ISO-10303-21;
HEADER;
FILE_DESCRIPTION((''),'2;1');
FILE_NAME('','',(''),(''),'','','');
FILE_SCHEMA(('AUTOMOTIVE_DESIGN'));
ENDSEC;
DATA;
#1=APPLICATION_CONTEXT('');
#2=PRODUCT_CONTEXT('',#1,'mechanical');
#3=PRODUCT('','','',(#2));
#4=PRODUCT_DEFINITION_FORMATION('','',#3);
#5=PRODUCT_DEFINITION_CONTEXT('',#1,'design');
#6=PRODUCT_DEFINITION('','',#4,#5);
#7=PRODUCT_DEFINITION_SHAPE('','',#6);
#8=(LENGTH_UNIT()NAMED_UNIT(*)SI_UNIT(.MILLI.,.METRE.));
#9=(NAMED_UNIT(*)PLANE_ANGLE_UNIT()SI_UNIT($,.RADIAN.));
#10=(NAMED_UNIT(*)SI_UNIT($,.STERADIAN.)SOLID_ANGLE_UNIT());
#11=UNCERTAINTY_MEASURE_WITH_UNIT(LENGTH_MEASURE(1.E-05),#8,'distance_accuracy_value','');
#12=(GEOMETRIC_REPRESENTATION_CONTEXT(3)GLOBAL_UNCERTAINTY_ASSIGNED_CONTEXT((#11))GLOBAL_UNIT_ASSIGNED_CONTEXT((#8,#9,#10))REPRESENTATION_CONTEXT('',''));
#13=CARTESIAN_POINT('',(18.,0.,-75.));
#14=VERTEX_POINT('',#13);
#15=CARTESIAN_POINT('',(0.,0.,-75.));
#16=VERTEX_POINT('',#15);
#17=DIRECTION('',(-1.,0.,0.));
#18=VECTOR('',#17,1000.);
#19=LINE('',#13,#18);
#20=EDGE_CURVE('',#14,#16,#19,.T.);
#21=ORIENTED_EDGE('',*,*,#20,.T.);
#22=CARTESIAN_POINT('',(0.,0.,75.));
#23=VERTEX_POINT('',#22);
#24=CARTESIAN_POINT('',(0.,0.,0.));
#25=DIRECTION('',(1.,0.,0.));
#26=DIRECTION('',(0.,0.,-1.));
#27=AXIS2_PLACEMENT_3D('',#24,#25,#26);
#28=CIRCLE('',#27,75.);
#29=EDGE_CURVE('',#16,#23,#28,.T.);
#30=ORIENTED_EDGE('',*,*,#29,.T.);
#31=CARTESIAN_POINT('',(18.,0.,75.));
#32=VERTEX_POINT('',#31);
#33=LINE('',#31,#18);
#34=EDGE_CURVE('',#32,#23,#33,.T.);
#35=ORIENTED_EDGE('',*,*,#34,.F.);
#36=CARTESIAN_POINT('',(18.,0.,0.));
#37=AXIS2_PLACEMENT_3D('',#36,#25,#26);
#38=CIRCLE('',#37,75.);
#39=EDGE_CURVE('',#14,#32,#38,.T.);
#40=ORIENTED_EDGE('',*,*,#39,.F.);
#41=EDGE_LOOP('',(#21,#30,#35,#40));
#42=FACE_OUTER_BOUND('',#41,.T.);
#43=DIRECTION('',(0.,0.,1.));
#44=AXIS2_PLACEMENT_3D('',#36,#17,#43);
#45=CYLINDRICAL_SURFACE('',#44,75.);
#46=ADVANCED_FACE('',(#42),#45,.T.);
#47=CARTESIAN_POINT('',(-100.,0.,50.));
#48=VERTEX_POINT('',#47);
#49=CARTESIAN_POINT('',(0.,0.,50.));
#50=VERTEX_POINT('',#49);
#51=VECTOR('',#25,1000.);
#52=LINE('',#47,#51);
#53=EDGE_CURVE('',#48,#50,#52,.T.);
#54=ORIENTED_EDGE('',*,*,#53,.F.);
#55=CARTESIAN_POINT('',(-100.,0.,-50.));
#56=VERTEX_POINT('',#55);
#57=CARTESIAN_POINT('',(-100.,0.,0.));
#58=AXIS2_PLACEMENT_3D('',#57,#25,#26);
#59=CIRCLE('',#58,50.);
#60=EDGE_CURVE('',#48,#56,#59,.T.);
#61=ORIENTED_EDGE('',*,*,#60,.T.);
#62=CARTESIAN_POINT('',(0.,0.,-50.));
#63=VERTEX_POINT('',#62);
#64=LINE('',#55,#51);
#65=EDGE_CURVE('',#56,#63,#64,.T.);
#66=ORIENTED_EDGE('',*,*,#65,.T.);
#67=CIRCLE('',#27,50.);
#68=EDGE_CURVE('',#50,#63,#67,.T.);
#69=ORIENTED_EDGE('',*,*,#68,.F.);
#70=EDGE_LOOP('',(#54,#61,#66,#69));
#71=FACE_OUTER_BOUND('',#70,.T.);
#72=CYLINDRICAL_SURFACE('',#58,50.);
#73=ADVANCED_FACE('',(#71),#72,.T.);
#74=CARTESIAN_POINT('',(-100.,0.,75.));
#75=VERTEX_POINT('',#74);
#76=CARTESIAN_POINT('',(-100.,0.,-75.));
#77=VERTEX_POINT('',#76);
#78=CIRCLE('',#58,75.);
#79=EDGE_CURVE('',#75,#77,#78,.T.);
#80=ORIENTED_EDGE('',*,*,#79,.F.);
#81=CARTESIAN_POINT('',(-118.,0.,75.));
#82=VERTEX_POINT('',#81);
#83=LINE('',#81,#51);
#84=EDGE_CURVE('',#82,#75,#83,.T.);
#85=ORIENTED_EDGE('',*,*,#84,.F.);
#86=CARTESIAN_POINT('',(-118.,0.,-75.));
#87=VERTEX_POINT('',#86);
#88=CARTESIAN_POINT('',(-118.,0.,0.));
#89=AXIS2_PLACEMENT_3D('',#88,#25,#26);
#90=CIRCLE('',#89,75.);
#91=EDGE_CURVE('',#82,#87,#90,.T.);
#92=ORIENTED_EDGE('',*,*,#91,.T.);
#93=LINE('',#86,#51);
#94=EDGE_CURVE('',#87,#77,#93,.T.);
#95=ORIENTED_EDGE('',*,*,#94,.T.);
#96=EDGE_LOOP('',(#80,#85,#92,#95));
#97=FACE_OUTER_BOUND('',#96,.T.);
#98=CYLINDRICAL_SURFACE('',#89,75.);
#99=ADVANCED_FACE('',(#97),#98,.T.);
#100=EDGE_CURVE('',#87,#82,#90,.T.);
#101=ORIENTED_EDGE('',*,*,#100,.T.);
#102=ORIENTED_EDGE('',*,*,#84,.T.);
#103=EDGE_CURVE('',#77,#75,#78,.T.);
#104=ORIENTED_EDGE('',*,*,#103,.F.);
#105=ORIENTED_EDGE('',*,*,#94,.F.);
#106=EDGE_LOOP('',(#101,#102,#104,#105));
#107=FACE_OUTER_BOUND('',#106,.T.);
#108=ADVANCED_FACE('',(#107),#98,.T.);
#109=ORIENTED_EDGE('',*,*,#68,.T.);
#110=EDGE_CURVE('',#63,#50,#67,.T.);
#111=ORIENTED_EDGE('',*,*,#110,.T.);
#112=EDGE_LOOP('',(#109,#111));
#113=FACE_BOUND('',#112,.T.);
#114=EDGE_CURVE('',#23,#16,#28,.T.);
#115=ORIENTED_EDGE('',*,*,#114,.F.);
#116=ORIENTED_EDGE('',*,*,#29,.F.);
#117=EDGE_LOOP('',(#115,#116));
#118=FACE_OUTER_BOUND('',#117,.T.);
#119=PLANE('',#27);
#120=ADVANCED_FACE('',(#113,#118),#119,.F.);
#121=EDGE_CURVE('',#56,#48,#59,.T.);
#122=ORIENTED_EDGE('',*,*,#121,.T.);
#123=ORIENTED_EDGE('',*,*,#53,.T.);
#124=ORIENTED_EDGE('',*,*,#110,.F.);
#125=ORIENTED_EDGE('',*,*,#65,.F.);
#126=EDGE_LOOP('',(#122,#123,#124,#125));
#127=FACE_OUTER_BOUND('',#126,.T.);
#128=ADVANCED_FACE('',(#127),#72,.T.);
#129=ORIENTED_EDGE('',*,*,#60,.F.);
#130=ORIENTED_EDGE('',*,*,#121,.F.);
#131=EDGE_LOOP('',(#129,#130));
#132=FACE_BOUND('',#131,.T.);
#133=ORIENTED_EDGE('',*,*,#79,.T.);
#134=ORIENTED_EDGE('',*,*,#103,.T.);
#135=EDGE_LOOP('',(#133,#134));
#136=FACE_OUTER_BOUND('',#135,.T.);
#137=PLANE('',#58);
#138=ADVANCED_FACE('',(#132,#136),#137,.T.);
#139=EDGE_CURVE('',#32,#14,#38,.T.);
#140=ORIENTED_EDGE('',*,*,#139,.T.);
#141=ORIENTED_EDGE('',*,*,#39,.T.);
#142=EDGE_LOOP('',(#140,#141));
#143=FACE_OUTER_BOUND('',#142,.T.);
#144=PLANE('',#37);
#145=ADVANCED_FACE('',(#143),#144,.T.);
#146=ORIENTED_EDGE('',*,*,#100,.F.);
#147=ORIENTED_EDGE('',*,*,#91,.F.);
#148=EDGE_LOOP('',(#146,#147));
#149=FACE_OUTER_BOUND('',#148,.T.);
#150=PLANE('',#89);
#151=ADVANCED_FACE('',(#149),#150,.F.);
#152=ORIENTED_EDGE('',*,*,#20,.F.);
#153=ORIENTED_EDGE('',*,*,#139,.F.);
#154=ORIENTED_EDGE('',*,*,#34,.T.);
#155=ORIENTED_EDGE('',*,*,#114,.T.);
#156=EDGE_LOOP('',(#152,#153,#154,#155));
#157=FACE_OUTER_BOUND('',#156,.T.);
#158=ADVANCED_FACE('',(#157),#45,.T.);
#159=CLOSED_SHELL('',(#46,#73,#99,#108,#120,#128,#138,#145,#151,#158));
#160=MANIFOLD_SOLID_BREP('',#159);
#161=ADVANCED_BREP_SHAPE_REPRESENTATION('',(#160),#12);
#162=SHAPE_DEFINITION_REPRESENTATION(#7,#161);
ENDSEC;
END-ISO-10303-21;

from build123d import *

# Parameters (mm, degrees)
SKETCH_1_4_R        = 75
BOSS_EXTRUDE1_DEPTH = 18
SKETCH_1_3_R        = 50
BOSS_EXTRUDE2_DEPTH = 100
BOSS_EXTRUDE3_START = -118
SKETCH_1_4_2_R      = 75
BOSS_EXTRUDE3_DEPTH = 18


with BuildPart() as part:
    # Sketch 1_4 → Boss-Extrude1 (new body)
    with BuildSketch(Plane(origin=(0, 0, 0), x_dir=(0, 0, -1), z_dir=(1, 0, 0))):
        Circle(SKETCH_1_4_R)
    extrude(amount=BOSS_EXTRUDE1_DEPTH)

    # 草图1<3> → Boss-Extrude2 (add)
    with BuildSketch(Plane(origin=(0, 0, 0), x_dir=(0, 0, -1), z_dir=(1, 0, 0))):
        Circle(SKETCH_1_3_R)
    extrude(amount=-BOSS_EXTRUDE2_DEPTH)

    # Sketch 1_4 2 → Boss-Extrude3 (add)
    with BuildSketch(Plane(origin=(0, 0, 0), x_dir=(0, 0, -1), z_dir=(1, 0, 0)).offset(BOSS_EXTRUDE3_START)):
        Circle(SKETCH_1_4_2_R)
    extrude(amount=BOSS_EXTRUDE3_DEPTH)


solid = part.part
